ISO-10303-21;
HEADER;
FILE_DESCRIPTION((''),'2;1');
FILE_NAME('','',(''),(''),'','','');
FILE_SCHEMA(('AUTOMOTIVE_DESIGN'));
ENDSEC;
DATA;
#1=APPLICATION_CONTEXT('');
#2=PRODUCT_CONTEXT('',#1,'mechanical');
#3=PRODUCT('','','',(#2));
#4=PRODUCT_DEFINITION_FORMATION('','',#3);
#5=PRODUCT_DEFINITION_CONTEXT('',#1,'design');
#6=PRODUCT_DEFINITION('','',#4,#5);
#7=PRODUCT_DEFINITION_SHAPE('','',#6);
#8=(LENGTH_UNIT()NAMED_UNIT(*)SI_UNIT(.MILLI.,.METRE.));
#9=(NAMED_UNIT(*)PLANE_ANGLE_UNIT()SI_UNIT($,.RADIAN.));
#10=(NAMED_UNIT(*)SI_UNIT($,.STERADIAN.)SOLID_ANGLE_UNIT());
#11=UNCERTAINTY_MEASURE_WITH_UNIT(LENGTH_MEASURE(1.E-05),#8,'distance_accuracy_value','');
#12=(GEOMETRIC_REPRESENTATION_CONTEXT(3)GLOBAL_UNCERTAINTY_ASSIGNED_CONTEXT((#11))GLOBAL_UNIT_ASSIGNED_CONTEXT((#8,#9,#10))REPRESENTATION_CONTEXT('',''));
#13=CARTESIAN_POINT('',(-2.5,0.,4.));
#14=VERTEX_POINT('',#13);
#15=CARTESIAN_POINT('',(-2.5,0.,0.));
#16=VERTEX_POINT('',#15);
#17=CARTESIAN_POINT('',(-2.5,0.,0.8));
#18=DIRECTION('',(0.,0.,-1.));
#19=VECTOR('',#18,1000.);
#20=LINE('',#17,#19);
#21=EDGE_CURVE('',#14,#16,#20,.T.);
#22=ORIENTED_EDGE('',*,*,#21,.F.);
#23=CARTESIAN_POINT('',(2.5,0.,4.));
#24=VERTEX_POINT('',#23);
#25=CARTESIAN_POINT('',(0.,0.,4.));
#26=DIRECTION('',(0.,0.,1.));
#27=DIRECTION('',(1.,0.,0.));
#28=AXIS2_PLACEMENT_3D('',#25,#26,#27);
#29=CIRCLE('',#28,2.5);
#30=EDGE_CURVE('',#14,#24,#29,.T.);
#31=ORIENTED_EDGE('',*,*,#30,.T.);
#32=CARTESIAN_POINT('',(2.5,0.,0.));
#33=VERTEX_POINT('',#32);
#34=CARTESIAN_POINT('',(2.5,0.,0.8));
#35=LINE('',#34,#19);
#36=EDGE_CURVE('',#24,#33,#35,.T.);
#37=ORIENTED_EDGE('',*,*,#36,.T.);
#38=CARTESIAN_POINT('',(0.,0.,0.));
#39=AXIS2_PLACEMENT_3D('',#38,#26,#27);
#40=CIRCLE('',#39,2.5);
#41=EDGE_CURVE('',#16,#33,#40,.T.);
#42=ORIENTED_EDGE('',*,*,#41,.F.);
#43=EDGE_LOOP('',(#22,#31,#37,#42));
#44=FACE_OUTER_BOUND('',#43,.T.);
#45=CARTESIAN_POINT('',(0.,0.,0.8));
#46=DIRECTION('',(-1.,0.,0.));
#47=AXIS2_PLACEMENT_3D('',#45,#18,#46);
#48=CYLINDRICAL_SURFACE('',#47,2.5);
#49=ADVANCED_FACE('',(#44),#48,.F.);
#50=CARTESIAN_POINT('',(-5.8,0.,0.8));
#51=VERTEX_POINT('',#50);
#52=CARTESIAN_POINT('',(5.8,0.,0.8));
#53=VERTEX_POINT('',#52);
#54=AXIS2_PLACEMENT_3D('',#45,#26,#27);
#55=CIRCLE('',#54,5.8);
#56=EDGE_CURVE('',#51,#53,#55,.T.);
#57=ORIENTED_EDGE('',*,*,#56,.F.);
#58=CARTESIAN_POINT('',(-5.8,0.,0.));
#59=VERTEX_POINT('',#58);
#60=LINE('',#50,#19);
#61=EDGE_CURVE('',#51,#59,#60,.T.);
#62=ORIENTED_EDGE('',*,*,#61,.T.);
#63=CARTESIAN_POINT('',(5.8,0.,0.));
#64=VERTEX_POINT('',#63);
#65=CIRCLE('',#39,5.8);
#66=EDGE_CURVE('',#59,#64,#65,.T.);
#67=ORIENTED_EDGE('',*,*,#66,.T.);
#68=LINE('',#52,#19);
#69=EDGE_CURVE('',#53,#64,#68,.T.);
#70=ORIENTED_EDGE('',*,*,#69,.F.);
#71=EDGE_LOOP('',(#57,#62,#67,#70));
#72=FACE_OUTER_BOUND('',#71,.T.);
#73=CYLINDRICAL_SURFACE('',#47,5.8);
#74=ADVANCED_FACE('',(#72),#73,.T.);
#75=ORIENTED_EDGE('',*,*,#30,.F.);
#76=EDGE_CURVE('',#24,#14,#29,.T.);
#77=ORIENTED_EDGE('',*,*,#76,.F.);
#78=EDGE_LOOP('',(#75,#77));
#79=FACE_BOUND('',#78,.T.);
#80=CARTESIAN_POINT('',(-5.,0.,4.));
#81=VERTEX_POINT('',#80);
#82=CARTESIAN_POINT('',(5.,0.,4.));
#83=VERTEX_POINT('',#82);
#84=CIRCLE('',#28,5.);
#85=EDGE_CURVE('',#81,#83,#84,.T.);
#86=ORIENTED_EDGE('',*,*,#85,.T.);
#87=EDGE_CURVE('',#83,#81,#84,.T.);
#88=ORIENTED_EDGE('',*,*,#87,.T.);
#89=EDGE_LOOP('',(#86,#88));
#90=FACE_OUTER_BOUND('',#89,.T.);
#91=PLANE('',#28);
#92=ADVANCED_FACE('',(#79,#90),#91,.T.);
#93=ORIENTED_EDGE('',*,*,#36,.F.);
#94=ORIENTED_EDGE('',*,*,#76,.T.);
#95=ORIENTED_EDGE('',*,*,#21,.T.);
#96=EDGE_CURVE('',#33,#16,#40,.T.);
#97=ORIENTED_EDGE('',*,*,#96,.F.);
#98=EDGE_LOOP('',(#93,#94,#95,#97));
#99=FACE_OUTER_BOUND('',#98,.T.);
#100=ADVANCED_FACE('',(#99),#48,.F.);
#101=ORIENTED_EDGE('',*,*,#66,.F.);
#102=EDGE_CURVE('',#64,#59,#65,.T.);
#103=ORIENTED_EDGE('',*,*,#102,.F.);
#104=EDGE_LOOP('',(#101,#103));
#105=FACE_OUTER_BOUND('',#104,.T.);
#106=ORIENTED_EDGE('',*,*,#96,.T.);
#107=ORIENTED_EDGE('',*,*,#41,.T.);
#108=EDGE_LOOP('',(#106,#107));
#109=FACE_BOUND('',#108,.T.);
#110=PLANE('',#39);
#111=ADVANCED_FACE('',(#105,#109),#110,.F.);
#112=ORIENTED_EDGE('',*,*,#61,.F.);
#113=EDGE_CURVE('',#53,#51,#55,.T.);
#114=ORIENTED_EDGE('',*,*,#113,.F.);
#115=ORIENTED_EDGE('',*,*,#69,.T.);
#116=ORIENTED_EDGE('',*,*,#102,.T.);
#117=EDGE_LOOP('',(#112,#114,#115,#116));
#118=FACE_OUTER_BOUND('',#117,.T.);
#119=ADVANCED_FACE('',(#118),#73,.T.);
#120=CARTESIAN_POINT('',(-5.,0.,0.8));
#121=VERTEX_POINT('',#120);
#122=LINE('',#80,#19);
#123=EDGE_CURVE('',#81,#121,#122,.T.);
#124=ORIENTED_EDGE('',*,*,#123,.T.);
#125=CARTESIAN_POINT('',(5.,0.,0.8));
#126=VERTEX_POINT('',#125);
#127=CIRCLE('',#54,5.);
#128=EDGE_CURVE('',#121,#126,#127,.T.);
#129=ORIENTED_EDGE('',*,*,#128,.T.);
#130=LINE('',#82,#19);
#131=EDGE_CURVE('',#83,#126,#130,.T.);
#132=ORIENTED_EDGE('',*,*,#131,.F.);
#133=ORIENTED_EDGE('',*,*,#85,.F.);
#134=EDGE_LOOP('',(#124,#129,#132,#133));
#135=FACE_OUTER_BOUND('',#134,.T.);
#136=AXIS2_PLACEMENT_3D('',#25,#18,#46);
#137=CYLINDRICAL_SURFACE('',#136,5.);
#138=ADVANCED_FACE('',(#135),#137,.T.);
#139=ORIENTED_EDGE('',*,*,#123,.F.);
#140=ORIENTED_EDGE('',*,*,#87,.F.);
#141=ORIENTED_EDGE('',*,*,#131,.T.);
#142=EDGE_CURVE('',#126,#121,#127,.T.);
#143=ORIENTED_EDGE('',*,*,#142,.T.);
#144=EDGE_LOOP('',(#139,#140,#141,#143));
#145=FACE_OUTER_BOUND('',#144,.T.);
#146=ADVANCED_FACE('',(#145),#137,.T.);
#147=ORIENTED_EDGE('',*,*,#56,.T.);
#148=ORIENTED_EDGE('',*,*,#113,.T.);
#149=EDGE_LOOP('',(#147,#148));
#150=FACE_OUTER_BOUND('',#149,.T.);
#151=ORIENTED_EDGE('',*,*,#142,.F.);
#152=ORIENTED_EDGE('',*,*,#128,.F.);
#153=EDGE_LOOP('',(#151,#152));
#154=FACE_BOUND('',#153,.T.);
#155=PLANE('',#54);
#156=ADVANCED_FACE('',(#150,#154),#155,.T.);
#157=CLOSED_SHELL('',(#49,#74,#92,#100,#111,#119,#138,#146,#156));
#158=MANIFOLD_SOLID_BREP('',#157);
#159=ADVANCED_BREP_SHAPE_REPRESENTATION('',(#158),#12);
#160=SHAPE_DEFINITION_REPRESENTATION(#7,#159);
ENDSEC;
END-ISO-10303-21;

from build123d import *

# Parameters (mm, degrees)
SKETCH_1_R      = 5.8
SKETCH_1_R_2    = 2.5
EXTRUDE_1_DEPTH = 0.8
SKETCH_2_R      = 5
SKETCH_2_R_2    = 2.5
EXTRUDE_2_DEPTH = 3.2


with BuildPart() as part:
    # 草图1 → 凸台-拉伸1 (new body)
    with BuildSketch(Plane.XY):
        Circle(SKETCH_1_R)
        Circle(SKETCH_1_R_2, mode=Mode.SUBTRACT)
    extrude(amount=EXTRUDE_1_DEPTH)

    # 草图2 → 凸台-拉伸2 (add)
    with BuildSketch(Plane.XY.offset(0.8)):
        Circle(SKETCH_2_R)
        Circle(SKETCH_2_R_2, mode=Mode.SUBTRACT)
    extrude(amount=EXTRUDE_2_DEPTH)


solid = part.part
